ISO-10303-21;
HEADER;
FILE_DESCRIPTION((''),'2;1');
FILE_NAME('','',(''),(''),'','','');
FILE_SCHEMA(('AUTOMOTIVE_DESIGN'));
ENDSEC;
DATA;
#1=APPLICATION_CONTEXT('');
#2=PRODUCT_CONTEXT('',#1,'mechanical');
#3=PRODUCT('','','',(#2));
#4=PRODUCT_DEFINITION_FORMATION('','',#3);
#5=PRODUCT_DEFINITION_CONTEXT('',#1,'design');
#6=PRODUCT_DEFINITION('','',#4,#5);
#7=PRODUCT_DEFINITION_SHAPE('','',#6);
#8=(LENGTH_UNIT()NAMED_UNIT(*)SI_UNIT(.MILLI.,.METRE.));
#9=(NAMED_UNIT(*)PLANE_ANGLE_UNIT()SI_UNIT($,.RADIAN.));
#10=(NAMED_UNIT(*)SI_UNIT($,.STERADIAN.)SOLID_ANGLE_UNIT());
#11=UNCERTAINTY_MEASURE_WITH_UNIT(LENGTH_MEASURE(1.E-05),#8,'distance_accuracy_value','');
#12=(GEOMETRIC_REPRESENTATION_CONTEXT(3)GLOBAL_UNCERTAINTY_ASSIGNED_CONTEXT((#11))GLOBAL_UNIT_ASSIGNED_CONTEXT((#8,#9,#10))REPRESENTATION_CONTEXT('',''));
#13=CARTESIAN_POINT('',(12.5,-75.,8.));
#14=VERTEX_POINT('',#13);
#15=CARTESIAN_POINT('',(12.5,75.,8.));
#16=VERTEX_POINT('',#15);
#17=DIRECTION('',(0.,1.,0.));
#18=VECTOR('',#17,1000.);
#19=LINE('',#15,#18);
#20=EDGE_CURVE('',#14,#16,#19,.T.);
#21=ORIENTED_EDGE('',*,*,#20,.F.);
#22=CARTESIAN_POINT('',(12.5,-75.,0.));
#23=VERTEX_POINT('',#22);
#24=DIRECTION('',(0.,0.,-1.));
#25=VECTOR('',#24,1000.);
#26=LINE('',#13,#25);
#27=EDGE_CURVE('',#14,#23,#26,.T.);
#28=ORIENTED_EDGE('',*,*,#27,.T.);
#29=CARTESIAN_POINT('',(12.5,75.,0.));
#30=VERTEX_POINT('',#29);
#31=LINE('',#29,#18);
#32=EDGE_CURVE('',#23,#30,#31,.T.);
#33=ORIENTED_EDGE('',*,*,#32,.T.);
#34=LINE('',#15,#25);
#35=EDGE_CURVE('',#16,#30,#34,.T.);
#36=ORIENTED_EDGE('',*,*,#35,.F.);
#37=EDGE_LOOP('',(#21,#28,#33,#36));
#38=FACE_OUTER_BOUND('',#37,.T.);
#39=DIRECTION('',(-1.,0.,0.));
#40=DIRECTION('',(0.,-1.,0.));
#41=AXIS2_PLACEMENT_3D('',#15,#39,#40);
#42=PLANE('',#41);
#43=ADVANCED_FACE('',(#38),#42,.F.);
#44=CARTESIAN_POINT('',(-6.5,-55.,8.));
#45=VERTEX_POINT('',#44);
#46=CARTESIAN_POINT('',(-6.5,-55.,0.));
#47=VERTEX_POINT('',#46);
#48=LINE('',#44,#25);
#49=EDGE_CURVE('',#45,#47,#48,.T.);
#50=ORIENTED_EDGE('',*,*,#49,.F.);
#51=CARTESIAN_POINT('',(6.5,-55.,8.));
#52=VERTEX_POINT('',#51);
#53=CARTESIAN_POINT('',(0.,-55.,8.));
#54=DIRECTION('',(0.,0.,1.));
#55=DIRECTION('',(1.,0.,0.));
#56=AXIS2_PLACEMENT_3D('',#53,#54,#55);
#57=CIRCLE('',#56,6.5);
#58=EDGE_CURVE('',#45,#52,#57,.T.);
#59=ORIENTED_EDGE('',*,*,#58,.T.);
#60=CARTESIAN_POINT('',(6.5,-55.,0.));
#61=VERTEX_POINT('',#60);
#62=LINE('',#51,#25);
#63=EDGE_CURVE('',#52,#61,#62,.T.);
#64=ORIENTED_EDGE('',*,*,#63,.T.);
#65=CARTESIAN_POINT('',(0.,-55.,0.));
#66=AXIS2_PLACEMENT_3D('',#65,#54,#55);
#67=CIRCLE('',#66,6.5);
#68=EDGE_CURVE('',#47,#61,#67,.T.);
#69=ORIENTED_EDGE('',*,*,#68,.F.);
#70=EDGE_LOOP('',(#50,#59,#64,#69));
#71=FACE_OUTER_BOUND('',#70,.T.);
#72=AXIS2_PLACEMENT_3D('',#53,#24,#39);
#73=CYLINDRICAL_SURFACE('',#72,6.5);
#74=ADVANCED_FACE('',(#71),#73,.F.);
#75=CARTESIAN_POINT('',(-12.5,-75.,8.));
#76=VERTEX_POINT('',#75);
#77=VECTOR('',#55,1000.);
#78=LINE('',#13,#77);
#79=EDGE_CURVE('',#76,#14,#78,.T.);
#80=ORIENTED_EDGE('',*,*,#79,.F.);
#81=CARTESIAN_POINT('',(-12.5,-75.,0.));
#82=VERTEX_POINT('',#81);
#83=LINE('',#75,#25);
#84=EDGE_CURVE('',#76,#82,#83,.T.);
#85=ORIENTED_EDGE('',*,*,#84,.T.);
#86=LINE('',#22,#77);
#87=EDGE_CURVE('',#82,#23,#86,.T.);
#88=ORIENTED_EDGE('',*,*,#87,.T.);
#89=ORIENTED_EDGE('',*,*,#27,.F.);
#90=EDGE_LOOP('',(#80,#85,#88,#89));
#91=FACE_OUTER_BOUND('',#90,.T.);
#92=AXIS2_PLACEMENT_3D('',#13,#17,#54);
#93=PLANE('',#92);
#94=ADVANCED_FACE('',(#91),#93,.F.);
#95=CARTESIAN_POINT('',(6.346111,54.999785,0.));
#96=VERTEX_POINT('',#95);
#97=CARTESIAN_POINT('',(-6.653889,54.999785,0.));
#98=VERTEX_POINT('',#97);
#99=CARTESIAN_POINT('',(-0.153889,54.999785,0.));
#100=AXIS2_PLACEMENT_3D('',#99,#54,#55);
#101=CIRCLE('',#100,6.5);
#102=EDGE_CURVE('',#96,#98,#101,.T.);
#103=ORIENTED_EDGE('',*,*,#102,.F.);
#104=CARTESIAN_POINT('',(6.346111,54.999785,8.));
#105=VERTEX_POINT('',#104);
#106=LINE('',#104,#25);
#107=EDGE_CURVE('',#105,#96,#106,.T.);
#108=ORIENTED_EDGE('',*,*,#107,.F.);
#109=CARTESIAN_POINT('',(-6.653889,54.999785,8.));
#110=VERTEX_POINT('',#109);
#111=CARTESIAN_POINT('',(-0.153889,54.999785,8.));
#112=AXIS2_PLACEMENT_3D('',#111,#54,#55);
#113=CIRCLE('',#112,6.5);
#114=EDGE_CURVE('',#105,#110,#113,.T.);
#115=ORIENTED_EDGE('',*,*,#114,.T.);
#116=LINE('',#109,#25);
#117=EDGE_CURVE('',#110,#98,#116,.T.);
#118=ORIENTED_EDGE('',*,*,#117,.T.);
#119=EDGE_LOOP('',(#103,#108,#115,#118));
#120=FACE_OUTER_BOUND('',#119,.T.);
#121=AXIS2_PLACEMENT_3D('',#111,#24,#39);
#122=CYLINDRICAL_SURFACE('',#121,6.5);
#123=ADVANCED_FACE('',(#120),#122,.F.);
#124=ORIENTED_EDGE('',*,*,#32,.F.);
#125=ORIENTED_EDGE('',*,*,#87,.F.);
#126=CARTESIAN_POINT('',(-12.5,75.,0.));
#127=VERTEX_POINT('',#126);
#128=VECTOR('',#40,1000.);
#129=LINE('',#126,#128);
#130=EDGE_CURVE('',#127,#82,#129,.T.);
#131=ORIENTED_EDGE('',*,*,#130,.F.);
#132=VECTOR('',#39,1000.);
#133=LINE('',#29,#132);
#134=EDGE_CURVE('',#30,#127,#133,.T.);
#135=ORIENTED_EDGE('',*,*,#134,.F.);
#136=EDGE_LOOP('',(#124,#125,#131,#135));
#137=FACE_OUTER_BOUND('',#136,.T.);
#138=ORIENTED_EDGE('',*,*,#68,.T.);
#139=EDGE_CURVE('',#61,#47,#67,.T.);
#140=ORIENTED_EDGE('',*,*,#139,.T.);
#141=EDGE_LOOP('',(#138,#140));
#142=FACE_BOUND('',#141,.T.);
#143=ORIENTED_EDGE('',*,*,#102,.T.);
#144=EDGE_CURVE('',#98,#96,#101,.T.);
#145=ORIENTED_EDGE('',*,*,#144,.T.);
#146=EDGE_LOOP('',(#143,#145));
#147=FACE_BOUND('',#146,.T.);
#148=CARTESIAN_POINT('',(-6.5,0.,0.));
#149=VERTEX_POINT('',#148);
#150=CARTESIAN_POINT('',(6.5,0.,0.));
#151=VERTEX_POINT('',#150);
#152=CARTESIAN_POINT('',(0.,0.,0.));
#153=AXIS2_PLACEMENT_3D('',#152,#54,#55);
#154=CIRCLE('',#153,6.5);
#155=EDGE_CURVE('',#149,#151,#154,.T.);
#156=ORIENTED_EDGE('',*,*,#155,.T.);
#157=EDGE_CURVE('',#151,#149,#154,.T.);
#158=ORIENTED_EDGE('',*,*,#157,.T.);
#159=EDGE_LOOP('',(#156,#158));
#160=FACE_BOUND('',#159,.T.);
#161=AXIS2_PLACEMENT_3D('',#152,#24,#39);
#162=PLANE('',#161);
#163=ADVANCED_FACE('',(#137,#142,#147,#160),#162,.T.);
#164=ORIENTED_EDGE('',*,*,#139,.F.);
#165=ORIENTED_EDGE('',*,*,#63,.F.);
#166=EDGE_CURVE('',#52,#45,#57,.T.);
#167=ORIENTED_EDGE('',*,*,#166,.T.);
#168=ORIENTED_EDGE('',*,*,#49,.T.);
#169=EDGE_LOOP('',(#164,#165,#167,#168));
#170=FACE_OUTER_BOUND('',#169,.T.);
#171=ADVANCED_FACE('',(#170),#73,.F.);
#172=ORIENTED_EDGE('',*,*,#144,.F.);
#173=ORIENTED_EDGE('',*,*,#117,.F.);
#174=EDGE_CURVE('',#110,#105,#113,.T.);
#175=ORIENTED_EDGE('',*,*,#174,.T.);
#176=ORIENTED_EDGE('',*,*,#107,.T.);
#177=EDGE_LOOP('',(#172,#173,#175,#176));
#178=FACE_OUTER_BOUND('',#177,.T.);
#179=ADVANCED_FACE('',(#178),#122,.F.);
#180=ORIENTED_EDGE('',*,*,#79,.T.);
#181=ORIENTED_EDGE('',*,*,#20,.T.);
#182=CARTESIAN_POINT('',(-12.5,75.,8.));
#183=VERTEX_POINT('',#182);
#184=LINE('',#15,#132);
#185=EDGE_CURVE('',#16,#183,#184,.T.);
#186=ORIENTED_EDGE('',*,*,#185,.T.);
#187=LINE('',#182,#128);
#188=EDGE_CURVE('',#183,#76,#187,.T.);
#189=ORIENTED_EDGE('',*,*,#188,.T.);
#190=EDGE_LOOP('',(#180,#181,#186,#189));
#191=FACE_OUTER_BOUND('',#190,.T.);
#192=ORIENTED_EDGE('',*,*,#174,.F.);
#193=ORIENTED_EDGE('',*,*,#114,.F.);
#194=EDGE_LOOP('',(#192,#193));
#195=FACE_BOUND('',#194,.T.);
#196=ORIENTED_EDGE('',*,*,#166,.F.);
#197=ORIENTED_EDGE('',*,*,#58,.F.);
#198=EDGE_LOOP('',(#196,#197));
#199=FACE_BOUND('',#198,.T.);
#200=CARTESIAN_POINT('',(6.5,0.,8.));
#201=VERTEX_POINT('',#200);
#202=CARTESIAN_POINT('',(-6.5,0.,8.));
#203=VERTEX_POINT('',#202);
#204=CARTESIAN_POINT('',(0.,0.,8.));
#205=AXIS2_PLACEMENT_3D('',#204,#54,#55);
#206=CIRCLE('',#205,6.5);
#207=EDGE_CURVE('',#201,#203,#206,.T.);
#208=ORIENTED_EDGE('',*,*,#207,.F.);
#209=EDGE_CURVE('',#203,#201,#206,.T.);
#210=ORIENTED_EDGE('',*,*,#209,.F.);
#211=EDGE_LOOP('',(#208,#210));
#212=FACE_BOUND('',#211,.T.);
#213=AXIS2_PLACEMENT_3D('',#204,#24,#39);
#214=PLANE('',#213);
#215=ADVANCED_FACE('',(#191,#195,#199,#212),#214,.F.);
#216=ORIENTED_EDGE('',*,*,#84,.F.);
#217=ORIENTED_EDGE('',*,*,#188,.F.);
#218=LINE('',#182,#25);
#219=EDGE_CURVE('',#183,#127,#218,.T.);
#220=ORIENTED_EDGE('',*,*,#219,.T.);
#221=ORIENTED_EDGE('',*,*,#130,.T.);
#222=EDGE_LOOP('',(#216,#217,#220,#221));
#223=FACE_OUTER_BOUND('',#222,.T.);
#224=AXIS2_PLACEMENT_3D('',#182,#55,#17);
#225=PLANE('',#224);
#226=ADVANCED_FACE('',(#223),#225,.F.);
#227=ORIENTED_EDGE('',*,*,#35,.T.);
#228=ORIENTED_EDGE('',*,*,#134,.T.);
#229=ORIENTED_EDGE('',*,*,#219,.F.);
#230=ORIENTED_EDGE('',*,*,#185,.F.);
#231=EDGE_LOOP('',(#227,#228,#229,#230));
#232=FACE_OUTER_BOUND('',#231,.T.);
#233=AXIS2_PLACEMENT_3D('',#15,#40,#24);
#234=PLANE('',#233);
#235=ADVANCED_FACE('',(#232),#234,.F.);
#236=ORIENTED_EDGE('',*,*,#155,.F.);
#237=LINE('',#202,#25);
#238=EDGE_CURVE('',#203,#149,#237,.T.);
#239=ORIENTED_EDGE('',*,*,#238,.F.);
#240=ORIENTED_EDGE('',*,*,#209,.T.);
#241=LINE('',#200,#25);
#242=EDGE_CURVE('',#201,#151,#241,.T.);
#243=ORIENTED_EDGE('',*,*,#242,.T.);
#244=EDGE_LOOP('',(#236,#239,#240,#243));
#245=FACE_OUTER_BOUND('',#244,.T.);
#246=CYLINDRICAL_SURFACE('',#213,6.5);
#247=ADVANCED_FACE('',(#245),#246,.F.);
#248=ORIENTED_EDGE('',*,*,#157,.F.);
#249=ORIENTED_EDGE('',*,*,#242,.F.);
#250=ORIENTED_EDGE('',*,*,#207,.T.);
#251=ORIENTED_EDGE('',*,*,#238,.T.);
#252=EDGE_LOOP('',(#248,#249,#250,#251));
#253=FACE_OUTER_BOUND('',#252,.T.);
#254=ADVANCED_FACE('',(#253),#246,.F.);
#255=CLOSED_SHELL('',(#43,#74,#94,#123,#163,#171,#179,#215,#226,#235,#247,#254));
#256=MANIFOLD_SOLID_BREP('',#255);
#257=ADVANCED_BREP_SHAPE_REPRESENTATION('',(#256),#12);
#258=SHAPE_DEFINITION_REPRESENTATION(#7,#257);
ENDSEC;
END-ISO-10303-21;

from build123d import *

# Parameters (mm, degrees)
SKETCH_1_W      = 25
SKETCH_1_H      = 150
SKETCH_1_R      = 6.5
EXTRUDE_1_DEPTH = 8


with BuildPart() as part:
    # 草图1 → 凸台-拉伸1 (new body)
    with BuildSketch(Plane.XY):
        Rectangle(SKETCH_1_W, SKETCH_1_H)
        with Locations((-0.153888597, 54.999784711)):
            Circle(SKETCH_1_R, mode=Mode.SUBTRACT)
        Circle(SKETCH_1_R, mode=Mode.SUBTRACT)
        with Locations((0, -55)):
            Circle(SKETCH_1_R, mode=Mode.SUBTRACT)
    extrude(amount=EXTRUDE_1_DEPTH)


solid = part.part
